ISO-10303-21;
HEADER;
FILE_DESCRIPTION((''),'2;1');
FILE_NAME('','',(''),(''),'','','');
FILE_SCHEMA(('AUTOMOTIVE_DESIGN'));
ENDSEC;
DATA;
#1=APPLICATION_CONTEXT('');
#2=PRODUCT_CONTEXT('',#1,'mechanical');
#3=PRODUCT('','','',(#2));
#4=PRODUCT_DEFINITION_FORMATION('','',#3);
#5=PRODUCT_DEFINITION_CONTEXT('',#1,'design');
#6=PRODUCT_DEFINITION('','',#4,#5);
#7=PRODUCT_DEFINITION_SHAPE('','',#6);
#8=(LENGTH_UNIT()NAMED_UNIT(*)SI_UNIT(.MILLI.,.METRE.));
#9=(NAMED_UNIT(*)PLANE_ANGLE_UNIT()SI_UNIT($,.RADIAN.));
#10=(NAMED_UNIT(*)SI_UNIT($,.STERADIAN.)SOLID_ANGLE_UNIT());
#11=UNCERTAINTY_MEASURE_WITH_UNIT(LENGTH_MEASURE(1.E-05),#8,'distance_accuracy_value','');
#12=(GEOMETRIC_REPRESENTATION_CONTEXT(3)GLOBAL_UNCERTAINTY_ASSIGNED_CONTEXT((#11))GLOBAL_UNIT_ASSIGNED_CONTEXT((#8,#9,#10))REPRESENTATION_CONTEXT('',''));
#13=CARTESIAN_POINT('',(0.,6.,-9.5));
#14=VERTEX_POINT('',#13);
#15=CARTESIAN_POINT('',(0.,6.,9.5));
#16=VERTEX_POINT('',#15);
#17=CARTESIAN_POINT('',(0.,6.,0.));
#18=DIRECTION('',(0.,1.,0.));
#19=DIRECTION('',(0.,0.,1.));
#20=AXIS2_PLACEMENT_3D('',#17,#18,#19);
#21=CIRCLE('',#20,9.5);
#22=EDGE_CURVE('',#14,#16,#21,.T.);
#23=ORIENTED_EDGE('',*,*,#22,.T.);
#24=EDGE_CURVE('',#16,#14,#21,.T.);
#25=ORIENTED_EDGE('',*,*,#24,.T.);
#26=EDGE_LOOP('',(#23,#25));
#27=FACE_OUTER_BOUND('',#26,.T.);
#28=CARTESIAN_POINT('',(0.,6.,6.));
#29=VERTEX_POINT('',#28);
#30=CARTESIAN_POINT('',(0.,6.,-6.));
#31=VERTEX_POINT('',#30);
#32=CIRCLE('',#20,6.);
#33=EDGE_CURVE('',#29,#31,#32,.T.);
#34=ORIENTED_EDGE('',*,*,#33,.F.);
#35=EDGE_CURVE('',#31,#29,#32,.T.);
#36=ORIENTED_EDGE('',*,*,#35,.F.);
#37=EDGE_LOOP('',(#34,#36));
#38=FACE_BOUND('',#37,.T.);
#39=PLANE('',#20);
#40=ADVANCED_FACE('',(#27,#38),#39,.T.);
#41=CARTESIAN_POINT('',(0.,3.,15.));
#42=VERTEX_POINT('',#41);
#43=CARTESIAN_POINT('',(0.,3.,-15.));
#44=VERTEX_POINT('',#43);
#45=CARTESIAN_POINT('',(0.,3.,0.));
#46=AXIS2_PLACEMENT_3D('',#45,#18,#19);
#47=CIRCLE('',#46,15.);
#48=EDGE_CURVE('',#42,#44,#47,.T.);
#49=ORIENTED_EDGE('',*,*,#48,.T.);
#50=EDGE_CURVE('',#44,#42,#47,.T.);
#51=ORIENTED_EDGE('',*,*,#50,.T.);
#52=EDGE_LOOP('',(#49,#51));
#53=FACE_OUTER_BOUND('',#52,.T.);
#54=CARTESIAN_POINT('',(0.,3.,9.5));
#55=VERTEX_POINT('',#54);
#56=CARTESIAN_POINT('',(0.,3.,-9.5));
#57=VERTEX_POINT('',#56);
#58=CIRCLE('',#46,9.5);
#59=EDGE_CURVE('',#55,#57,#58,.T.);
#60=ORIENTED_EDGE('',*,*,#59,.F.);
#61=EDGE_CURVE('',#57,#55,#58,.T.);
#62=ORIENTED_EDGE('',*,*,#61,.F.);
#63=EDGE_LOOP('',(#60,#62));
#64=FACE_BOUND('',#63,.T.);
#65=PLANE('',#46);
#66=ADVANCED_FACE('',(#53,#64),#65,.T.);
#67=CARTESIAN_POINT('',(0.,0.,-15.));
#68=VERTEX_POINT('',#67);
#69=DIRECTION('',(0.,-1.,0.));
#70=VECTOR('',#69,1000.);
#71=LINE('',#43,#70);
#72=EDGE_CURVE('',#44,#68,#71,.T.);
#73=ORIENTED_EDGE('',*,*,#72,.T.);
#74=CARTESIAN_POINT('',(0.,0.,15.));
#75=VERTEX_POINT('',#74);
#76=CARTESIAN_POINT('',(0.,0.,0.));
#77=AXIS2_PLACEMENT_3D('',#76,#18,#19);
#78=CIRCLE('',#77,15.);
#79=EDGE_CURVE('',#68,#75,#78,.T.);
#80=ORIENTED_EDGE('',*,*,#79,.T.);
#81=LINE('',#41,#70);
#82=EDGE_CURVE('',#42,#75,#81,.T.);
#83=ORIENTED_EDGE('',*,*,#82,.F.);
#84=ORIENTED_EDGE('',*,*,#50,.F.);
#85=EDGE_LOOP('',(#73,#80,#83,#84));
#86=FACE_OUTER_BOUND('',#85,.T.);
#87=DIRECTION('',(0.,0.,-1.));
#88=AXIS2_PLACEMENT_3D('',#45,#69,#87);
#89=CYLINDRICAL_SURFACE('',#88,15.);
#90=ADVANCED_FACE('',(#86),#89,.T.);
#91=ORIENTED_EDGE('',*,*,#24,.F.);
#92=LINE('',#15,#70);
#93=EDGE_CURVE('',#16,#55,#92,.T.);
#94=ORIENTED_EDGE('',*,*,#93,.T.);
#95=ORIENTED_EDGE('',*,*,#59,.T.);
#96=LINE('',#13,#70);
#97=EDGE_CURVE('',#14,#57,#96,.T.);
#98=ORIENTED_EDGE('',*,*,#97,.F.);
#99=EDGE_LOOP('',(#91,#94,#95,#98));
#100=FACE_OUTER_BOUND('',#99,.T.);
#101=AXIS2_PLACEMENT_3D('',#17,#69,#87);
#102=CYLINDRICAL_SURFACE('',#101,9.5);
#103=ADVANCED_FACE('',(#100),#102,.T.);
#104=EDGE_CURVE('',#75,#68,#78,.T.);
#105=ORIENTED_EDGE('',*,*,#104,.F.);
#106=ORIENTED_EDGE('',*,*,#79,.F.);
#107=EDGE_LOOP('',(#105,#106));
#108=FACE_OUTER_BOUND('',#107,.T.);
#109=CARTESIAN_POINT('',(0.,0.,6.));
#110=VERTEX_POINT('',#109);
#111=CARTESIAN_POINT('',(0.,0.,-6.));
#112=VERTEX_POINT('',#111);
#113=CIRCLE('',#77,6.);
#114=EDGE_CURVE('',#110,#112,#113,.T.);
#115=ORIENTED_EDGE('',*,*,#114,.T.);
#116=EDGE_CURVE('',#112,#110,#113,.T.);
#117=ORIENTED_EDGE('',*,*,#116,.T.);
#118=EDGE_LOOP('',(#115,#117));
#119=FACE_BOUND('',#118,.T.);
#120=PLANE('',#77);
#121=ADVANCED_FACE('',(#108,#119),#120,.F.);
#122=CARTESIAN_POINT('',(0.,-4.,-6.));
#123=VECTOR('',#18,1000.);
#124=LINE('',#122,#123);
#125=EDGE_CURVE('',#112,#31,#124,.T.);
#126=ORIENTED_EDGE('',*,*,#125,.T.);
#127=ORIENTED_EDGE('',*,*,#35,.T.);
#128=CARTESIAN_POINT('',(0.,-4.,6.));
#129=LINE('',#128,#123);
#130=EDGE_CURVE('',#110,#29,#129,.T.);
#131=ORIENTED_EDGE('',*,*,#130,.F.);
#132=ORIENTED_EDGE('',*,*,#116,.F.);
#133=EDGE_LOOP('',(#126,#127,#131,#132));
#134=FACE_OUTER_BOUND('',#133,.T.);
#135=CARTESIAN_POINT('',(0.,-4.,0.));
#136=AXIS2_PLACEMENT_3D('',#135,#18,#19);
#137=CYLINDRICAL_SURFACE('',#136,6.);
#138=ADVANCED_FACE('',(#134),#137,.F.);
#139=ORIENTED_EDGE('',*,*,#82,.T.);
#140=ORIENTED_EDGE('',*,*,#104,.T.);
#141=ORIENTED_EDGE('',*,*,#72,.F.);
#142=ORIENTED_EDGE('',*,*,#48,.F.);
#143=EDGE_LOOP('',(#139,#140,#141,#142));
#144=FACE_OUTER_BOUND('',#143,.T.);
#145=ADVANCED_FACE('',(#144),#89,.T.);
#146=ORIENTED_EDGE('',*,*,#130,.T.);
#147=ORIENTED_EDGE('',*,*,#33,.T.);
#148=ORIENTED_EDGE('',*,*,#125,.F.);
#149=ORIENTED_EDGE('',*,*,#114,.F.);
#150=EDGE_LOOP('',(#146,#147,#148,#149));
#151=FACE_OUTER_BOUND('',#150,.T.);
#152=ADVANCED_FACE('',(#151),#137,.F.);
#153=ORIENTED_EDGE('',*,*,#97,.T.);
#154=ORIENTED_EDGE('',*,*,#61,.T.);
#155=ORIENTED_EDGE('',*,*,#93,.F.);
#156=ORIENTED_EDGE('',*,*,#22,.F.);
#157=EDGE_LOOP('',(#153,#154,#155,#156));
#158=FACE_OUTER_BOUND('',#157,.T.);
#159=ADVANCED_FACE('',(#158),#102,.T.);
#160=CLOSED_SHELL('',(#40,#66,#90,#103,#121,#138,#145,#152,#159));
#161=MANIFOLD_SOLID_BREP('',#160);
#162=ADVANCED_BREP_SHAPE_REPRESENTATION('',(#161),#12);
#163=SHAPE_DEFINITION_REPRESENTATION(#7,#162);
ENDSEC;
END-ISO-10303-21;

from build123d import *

# Parameters (mm, degrees)
SKETCH1_R           = 15
BOSS_EXTRUDE1_DEPTH = 3
SKETCH2_R           = 9.5
BOSS_EXTRUDE2_DEPTH = 3
SKETCH3_R           = 6
CUT_EXTRUDE1_DEPTH  = 10


with BuildPart() as part:
    # Sketch1 → Boss-Extrude1 (new body)
    with BuildSketch(Plane(origin=(0, 0, 0), x_dir=(1, 0, 0), z_dir=(0, 1, 0))):
        with Locations(Location((0, 0, 0), (0, 0, 270))):
            Circle(SKETCH1_R)
    extrude(amount=BOSS_EXTRUDE1_DEPTH)

    # Sketch2 → Boss-Extrude2 (add)
    with BuildSketch(Plane(origin=(0, 3, 0), x_dir=(1, 0, 0), z_dir=(0, 1, 0))):
        with Locations(Location((0, 0, 0), (0, 0, 270))):
            Circle(SKETCH2_R)
    extrude(amount=BOSS_EXTRUDE2_DEPTH)

    # Sketch3 → Cut-Extrude1 (cut)
    with BuildSketch(Plane(origin=(0, 6, 0), x_dir=(1, 0, 0), z_dir=(0, 1, 0))):
        with Locations(Location((0, 0, 0), (0, 0, 270))):
            Circle(SKETCH3_R)
    extrude(amount=-CUT_EXTRUDE1_DEPTH, mode=Mode.SUBTRACT)


solid = part.part
